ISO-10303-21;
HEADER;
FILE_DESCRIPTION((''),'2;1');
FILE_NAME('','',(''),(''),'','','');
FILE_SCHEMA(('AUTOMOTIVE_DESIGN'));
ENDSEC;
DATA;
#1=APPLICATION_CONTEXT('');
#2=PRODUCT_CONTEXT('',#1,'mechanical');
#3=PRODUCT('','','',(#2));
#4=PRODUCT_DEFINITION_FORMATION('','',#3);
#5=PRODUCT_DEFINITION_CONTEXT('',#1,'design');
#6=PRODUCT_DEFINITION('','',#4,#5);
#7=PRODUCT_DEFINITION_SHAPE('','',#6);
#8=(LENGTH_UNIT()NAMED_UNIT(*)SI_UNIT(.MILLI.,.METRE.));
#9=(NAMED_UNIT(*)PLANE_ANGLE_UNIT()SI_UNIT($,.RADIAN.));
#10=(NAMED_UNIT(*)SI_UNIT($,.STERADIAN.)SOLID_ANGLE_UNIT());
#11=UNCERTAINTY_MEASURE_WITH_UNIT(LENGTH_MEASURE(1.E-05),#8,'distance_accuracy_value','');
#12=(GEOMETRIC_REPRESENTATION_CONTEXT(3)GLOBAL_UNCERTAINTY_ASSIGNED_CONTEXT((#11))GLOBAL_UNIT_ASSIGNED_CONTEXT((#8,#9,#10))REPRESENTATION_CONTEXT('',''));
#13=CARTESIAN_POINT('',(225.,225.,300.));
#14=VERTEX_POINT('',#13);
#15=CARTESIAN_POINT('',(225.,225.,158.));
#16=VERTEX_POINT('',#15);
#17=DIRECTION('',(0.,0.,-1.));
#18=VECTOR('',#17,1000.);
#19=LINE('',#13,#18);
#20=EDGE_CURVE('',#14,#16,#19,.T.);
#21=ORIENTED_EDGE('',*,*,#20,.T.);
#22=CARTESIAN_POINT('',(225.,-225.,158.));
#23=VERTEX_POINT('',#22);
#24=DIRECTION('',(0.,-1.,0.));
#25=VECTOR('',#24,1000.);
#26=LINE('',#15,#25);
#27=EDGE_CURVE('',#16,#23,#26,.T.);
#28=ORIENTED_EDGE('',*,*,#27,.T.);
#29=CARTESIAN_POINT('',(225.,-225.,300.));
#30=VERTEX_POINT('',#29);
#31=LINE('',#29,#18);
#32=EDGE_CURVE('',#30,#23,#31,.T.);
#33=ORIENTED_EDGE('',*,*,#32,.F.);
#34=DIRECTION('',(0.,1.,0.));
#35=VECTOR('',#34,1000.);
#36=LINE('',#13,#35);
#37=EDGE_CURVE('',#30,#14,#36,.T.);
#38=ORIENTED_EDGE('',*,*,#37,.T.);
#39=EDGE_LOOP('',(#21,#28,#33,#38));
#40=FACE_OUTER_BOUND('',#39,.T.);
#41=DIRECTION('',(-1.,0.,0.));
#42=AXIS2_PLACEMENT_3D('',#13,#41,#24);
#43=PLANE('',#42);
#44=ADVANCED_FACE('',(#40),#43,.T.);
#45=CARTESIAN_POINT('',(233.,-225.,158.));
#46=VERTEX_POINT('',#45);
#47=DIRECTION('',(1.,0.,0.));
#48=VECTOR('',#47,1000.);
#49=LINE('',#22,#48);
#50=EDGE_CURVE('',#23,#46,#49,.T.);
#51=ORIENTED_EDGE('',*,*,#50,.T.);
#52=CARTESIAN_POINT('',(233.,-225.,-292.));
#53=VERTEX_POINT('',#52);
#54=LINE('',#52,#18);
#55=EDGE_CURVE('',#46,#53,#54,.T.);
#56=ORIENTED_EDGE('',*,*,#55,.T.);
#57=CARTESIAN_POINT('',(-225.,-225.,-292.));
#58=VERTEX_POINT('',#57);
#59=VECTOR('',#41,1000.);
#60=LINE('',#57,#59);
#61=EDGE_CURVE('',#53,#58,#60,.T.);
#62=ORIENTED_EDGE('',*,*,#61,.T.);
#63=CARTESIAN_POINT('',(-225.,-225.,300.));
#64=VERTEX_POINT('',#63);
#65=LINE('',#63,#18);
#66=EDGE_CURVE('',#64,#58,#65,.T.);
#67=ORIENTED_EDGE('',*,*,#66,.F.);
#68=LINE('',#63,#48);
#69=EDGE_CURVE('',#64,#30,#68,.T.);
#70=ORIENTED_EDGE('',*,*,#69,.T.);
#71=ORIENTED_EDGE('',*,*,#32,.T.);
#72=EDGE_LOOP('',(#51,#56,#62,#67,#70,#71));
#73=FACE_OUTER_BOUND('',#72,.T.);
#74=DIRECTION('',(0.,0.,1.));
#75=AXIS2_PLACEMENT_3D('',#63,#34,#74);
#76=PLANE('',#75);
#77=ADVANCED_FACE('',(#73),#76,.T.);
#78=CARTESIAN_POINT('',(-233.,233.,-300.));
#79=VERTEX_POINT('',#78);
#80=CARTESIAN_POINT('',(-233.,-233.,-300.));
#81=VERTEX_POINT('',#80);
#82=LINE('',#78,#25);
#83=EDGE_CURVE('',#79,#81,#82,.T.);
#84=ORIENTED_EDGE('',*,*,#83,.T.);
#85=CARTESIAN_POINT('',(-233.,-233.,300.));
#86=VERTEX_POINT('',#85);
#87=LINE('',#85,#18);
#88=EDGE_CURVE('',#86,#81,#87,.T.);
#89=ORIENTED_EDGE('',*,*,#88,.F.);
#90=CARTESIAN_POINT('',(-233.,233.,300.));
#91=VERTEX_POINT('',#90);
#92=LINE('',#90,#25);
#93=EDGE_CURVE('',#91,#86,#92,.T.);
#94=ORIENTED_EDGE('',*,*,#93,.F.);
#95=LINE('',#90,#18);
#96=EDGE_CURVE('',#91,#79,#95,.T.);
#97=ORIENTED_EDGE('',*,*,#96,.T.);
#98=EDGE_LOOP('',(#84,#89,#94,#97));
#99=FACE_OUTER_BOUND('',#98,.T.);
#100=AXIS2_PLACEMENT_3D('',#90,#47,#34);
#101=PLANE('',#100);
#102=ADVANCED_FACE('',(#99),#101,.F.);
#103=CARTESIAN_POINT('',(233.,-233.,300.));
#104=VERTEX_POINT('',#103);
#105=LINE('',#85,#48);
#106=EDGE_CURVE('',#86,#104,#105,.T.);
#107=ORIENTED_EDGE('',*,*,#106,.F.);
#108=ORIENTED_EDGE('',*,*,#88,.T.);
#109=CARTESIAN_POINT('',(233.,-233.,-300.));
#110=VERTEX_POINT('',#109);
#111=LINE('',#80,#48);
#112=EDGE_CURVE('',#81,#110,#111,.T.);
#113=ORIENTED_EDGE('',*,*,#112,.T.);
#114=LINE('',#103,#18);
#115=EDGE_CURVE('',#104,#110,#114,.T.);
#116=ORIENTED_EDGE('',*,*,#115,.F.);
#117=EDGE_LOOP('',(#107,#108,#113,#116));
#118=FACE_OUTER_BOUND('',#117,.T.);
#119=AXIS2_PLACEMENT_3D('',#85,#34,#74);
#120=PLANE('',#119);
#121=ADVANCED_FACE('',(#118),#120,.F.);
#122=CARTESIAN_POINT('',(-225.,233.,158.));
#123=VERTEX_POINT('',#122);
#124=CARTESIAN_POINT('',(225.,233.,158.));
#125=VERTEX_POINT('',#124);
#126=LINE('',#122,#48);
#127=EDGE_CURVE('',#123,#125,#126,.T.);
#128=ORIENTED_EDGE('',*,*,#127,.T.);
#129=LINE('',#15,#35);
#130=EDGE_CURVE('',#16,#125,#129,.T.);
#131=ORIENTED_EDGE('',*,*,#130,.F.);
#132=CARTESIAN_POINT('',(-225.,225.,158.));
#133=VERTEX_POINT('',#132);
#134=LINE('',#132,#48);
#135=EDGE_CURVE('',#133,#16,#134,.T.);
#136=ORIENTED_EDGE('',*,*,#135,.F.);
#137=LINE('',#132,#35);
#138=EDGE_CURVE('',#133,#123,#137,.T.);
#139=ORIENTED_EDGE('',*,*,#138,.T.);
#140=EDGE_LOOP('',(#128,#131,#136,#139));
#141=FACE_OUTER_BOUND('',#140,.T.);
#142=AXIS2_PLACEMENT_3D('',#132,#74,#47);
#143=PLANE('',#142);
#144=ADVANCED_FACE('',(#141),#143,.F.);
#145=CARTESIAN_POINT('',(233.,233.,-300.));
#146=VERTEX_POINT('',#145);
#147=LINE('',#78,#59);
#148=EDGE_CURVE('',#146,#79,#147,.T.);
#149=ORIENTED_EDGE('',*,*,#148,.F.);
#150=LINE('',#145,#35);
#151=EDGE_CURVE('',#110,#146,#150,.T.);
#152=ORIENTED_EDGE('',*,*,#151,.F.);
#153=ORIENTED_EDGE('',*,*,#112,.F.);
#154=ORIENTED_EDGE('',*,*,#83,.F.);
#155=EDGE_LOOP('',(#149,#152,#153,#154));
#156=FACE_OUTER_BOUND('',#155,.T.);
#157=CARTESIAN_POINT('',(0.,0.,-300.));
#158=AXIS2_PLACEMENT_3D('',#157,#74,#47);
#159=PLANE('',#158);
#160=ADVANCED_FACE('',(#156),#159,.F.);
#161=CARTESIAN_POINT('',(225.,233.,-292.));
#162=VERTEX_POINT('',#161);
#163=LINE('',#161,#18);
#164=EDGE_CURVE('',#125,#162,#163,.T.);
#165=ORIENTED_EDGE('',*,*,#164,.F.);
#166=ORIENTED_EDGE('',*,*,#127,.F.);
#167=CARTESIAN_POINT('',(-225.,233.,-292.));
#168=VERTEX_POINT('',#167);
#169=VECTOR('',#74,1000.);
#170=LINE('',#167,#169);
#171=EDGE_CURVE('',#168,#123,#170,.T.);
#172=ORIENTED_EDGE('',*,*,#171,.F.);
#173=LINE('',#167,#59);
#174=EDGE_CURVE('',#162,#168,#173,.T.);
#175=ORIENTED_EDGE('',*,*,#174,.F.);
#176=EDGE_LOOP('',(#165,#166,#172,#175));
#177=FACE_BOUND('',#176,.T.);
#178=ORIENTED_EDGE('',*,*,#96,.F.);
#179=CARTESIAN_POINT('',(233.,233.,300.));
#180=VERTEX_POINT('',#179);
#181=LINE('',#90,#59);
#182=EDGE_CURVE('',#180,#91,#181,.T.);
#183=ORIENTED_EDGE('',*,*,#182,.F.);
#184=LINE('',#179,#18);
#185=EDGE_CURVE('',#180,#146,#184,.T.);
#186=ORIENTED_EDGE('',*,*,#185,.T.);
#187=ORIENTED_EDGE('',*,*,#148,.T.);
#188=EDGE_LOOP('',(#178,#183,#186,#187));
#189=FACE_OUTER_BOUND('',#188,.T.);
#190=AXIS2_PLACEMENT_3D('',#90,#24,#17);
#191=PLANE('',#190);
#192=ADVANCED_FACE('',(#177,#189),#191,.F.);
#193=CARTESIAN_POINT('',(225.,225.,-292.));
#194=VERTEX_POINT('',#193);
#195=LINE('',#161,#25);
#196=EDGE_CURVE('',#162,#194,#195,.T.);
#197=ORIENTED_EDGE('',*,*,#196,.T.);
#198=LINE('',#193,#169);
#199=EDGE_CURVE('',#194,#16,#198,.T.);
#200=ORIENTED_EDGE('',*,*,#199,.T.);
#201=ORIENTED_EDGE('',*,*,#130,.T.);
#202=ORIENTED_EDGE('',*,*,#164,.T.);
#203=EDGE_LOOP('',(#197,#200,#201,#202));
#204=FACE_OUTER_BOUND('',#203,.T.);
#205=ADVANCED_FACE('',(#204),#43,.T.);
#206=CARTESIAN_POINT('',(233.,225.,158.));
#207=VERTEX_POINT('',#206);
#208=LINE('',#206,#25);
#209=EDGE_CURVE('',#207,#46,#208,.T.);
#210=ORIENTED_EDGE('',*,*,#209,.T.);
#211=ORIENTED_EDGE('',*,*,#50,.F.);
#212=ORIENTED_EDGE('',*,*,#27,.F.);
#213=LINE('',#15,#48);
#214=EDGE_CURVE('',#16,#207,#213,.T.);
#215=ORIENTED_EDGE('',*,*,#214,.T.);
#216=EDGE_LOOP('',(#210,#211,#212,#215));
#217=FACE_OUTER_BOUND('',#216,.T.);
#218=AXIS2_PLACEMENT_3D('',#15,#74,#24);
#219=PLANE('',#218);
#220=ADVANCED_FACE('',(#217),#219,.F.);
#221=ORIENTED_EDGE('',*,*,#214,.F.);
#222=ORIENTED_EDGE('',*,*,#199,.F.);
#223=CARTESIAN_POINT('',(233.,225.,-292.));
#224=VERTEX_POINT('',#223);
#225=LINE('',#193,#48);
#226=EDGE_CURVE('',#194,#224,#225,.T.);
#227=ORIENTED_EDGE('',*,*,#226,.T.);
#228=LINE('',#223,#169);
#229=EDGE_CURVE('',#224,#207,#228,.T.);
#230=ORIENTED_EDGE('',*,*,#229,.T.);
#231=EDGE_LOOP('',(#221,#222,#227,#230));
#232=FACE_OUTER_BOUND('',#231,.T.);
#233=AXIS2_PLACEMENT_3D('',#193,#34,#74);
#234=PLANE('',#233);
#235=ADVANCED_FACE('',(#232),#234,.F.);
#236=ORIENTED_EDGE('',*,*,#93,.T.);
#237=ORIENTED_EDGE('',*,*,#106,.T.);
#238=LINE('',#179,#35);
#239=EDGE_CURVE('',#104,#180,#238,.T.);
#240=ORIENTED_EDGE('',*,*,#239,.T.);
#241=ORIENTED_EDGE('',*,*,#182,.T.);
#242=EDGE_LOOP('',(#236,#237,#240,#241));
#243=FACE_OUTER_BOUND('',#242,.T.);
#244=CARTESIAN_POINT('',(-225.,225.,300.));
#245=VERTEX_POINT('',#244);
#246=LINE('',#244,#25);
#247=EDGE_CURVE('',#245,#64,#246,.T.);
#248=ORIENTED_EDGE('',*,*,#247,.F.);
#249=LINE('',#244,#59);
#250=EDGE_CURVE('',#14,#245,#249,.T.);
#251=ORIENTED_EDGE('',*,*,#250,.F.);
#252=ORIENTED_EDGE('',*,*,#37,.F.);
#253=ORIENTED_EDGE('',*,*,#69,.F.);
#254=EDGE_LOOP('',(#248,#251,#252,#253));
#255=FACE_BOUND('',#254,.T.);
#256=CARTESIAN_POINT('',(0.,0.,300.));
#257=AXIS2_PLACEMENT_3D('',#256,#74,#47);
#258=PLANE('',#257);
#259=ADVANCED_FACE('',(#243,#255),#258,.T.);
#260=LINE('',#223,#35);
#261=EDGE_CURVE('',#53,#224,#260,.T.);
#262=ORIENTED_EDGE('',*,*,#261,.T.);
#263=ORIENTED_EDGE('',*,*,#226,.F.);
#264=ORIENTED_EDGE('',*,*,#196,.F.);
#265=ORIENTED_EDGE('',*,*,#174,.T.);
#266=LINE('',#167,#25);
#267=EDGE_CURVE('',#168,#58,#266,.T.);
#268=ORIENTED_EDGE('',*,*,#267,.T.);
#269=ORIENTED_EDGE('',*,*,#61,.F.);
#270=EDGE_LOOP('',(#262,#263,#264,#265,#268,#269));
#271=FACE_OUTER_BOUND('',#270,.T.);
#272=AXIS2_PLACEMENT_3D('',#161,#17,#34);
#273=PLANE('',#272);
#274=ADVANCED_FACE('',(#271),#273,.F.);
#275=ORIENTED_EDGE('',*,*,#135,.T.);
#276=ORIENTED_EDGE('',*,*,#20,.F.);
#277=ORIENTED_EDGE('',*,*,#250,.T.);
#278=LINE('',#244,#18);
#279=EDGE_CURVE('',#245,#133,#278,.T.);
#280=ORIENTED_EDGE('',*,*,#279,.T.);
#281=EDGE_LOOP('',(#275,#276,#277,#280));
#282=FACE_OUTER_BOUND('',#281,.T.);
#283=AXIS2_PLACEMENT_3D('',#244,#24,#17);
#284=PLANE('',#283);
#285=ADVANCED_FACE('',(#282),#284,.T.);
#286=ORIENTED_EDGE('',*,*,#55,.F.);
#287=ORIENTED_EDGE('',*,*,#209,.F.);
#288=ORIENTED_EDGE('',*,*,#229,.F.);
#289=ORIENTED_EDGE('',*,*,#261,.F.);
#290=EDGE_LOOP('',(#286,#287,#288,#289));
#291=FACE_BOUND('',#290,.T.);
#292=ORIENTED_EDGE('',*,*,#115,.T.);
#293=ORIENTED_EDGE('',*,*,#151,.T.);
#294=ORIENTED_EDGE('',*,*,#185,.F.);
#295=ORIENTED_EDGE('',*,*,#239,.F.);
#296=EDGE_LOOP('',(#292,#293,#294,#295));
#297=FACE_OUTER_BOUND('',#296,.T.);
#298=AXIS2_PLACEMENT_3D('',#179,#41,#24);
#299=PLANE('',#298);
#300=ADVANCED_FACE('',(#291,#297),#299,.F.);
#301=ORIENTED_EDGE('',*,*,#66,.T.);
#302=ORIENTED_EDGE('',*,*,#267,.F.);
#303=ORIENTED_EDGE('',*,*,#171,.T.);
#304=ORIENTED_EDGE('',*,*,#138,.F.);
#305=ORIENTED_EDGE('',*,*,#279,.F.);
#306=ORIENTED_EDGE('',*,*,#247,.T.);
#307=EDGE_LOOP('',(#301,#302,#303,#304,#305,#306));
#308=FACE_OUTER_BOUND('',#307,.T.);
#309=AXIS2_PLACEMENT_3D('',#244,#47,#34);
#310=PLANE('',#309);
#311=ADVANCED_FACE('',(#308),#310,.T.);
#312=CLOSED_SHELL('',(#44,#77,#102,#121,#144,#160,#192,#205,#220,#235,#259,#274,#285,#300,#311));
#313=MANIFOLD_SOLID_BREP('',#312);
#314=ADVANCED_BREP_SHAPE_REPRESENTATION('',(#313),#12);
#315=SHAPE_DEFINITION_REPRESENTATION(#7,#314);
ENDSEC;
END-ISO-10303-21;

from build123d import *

# Parameters (mm, degrees)
SKETCH2_W           = 466
SKETCH2_H           = 466
SKETCH2_W_2         = 450
SKETCH2_H_2         = 450
BOSS_EXTRUDE1_DEPTH = 300
SKETCH4_W           = 8
SKETCH4_H           = 466
BOSS_EXTRUDE2_DEPTH = 450
SKETCH5_W           = 450
SKETCH5_H           = 450
CUT_EXTRUDE1_DEPTH  = 8
SKETCH6_W           = 450
SKETCH6_H           = 450
CUT_EXTRUDE2_DEPTH  = 8


with BuildPart() as part:
    # Sketch2 → Boss-Extrude1 (new, symmetric)
    with BuildSketch(Plane.XY):
        Rectangle(SKETCH2_W, SKETCH2_H)
        Rectangle(SKETCH2_W_2, SKETCH2_H_2, mode=Mode.SUBTRACT)
    extrude(amount=BOSS_EXTRUDE1_DEPTH, both=True)

    # Sketch4 → Boss-Extrude2 (add)
    with BuildSketch(Plane(origin=(-225, 0, 0), x_dir=(0, 0, -1), z_dir=(1, 0, 0))):
        with Locations((296, 0)):
            Rectangle(SKETCH4_W, SKETCH4_H)
    extrude(amount=BOSS_EXTRUDE2_DEPTH)

    # Sketch5 → Cut-Extrude1 (cut)
    with BuildSketch(Plane(origin=(0, 233, 0), x_dir=(1, 0, 0), z_dir=(0, 1, 0))):
        with Locations((0, 67)):
            Rectangle(SKETCH5_W, SKETCH5_H)
    extrude(amount=-CUT_EXTRUDE1_DEPTH, mode=Mode.SUBTRACT)

    # Sketch6 → Cut-Extrude2 (cut)
    with BuildSketch(Plane(origin=(233, 0, 0), x_dir=(0, 0, -1), z_dir=(1, 0, 0))):
        with Locations((67, 0)):
            Rectangle(SKETCH6_W, SKETCH6_H)
    extrude(amount=-CUT_EXTRUDE2_DEPTH, mode=Mode.SUBTRACT)


solid = part.part
